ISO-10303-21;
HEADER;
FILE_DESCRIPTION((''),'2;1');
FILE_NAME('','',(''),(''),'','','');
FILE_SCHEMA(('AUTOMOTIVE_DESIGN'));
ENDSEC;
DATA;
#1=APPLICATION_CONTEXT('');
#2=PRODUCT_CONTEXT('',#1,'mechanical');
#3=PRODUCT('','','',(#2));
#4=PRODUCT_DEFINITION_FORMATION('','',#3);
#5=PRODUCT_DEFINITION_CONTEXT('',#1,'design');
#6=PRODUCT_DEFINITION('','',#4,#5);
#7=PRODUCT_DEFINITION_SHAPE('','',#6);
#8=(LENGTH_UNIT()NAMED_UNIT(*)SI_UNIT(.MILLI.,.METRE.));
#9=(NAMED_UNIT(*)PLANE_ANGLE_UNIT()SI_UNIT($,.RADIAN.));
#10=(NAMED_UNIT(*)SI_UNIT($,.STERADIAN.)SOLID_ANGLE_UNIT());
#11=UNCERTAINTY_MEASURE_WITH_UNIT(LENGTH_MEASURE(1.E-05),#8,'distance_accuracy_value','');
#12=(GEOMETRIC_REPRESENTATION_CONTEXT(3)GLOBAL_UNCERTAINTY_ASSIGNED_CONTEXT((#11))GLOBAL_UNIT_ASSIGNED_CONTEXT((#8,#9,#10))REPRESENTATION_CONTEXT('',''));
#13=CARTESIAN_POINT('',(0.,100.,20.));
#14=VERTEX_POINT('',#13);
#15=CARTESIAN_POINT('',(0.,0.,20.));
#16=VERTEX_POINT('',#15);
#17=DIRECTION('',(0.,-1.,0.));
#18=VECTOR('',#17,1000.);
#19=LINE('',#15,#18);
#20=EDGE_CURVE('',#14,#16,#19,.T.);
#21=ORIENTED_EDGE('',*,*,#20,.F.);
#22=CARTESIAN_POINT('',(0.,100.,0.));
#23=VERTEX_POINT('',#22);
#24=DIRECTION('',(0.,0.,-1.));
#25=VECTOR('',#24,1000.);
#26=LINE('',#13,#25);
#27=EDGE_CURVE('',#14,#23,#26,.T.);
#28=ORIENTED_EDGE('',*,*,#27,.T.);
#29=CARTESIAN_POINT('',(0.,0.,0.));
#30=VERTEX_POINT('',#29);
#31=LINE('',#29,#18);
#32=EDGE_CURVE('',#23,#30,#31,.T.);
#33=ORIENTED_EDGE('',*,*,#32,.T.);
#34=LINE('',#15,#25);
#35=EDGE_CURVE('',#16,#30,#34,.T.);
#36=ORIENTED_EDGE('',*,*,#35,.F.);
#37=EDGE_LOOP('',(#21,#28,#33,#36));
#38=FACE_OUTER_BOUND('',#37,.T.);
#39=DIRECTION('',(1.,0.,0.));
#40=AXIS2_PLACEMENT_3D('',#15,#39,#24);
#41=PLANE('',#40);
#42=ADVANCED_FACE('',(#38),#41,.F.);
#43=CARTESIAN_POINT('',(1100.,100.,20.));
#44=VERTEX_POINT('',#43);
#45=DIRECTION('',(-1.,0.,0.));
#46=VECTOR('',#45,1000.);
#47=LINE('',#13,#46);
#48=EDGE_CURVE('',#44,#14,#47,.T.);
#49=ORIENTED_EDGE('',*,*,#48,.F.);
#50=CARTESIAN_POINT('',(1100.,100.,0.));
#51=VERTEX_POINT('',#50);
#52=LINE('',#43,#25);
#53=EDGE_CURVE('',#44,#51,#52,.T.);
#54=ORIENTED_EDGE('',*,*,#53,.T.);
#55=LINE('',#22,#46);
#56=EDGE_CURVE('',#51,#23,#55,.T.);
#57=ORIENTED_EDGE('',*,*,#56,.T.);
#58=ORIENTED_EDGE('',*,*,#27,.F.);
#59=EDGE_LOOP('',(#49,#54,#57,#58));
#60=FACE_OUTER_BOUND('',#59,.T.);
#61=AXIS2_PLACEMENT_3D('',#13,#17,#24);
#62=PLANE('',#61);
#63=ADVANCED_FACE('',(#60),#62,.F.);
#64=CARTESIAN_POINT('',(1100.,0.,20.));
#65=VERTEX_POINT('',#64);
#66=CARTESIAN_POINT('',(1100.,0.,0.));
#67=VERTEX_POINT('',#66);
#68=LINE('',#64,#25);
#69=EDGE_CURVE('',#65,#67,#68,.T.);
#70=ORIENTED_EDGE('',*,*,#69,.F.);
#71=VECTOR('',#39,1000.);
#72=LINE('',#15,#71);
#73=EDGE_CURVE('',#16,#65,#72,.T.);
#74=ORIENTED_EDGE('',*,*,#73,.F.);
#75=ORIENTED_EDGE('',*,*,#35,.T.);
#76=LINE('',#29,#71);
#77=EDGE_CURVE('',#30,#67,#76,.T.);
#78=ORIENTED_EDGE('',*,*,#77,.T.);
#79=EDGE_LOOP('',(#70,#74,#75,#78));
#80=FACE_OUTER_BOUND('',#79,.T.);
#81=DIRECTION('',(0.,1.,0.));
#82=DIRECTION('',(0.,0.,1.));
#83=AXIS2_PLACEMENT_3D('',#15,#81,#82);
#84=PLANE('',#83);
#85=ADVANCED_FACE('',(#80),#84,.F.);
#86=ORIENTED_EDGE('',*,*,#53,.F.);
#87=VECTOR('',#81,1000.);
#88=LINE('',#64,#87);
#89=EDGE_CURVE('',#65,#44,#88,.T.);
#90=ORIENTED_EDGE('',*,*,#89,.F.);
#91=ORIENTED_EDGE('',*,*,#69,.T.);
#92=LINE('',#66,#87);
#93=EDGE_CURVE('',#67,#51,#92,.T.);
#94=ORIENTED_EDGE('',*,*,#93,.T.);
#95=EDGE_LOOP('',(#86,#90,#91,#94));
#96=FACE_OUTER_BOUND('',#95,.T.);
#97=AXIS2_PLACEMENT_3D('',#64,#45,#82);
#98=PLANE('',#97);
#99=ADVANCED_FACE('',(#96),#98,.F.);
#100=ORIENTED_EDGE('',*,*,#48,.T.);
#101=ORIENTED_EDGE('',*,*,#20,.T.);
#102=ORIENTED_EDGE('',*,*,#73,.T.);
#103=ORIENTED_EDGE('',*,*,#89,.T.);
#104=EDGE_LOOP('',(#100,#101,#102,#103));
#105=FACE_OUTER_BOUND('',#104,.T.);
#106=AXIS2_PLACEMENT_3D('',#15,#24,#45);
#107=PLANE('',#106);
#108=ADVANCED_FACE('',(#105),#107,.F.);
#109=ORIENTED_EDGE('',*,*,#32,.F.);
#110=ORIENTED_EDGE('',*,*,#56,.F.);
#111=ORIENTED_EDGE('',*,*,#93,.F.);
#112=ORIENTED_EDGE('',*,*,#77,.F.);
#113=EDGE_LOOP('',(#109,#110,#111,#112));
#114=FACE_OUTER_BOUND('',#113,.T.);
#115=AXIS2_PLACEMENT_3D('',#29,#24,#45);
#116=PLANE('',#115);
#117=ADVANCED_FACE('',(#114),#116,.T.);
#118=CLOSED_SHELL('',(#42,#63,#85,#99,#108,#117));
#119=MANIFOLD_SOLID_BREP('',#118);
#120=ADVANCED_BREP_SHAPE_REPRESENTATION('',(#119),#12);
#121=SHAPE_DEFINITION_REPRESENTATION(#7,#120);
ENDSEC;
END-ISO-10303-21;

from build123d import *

# Parameters (mm, degrees)
SKETCH1_W           = 1100
SKETCH1_H           = 100
BOSS_EXTRUDE1_DEPTH = 20


with BuildPart() as part:
    # Sketch1 → Boss-Extrude1 (new body)
    with BuildSketch(Plane.XY):
        with Locations((550, 50)):
            Rectangle(SKETCH1_W, SKETCH1_H)
    extrude(amount=BOSS_EXTRUDE1_DEPTH)


solid = part.part
